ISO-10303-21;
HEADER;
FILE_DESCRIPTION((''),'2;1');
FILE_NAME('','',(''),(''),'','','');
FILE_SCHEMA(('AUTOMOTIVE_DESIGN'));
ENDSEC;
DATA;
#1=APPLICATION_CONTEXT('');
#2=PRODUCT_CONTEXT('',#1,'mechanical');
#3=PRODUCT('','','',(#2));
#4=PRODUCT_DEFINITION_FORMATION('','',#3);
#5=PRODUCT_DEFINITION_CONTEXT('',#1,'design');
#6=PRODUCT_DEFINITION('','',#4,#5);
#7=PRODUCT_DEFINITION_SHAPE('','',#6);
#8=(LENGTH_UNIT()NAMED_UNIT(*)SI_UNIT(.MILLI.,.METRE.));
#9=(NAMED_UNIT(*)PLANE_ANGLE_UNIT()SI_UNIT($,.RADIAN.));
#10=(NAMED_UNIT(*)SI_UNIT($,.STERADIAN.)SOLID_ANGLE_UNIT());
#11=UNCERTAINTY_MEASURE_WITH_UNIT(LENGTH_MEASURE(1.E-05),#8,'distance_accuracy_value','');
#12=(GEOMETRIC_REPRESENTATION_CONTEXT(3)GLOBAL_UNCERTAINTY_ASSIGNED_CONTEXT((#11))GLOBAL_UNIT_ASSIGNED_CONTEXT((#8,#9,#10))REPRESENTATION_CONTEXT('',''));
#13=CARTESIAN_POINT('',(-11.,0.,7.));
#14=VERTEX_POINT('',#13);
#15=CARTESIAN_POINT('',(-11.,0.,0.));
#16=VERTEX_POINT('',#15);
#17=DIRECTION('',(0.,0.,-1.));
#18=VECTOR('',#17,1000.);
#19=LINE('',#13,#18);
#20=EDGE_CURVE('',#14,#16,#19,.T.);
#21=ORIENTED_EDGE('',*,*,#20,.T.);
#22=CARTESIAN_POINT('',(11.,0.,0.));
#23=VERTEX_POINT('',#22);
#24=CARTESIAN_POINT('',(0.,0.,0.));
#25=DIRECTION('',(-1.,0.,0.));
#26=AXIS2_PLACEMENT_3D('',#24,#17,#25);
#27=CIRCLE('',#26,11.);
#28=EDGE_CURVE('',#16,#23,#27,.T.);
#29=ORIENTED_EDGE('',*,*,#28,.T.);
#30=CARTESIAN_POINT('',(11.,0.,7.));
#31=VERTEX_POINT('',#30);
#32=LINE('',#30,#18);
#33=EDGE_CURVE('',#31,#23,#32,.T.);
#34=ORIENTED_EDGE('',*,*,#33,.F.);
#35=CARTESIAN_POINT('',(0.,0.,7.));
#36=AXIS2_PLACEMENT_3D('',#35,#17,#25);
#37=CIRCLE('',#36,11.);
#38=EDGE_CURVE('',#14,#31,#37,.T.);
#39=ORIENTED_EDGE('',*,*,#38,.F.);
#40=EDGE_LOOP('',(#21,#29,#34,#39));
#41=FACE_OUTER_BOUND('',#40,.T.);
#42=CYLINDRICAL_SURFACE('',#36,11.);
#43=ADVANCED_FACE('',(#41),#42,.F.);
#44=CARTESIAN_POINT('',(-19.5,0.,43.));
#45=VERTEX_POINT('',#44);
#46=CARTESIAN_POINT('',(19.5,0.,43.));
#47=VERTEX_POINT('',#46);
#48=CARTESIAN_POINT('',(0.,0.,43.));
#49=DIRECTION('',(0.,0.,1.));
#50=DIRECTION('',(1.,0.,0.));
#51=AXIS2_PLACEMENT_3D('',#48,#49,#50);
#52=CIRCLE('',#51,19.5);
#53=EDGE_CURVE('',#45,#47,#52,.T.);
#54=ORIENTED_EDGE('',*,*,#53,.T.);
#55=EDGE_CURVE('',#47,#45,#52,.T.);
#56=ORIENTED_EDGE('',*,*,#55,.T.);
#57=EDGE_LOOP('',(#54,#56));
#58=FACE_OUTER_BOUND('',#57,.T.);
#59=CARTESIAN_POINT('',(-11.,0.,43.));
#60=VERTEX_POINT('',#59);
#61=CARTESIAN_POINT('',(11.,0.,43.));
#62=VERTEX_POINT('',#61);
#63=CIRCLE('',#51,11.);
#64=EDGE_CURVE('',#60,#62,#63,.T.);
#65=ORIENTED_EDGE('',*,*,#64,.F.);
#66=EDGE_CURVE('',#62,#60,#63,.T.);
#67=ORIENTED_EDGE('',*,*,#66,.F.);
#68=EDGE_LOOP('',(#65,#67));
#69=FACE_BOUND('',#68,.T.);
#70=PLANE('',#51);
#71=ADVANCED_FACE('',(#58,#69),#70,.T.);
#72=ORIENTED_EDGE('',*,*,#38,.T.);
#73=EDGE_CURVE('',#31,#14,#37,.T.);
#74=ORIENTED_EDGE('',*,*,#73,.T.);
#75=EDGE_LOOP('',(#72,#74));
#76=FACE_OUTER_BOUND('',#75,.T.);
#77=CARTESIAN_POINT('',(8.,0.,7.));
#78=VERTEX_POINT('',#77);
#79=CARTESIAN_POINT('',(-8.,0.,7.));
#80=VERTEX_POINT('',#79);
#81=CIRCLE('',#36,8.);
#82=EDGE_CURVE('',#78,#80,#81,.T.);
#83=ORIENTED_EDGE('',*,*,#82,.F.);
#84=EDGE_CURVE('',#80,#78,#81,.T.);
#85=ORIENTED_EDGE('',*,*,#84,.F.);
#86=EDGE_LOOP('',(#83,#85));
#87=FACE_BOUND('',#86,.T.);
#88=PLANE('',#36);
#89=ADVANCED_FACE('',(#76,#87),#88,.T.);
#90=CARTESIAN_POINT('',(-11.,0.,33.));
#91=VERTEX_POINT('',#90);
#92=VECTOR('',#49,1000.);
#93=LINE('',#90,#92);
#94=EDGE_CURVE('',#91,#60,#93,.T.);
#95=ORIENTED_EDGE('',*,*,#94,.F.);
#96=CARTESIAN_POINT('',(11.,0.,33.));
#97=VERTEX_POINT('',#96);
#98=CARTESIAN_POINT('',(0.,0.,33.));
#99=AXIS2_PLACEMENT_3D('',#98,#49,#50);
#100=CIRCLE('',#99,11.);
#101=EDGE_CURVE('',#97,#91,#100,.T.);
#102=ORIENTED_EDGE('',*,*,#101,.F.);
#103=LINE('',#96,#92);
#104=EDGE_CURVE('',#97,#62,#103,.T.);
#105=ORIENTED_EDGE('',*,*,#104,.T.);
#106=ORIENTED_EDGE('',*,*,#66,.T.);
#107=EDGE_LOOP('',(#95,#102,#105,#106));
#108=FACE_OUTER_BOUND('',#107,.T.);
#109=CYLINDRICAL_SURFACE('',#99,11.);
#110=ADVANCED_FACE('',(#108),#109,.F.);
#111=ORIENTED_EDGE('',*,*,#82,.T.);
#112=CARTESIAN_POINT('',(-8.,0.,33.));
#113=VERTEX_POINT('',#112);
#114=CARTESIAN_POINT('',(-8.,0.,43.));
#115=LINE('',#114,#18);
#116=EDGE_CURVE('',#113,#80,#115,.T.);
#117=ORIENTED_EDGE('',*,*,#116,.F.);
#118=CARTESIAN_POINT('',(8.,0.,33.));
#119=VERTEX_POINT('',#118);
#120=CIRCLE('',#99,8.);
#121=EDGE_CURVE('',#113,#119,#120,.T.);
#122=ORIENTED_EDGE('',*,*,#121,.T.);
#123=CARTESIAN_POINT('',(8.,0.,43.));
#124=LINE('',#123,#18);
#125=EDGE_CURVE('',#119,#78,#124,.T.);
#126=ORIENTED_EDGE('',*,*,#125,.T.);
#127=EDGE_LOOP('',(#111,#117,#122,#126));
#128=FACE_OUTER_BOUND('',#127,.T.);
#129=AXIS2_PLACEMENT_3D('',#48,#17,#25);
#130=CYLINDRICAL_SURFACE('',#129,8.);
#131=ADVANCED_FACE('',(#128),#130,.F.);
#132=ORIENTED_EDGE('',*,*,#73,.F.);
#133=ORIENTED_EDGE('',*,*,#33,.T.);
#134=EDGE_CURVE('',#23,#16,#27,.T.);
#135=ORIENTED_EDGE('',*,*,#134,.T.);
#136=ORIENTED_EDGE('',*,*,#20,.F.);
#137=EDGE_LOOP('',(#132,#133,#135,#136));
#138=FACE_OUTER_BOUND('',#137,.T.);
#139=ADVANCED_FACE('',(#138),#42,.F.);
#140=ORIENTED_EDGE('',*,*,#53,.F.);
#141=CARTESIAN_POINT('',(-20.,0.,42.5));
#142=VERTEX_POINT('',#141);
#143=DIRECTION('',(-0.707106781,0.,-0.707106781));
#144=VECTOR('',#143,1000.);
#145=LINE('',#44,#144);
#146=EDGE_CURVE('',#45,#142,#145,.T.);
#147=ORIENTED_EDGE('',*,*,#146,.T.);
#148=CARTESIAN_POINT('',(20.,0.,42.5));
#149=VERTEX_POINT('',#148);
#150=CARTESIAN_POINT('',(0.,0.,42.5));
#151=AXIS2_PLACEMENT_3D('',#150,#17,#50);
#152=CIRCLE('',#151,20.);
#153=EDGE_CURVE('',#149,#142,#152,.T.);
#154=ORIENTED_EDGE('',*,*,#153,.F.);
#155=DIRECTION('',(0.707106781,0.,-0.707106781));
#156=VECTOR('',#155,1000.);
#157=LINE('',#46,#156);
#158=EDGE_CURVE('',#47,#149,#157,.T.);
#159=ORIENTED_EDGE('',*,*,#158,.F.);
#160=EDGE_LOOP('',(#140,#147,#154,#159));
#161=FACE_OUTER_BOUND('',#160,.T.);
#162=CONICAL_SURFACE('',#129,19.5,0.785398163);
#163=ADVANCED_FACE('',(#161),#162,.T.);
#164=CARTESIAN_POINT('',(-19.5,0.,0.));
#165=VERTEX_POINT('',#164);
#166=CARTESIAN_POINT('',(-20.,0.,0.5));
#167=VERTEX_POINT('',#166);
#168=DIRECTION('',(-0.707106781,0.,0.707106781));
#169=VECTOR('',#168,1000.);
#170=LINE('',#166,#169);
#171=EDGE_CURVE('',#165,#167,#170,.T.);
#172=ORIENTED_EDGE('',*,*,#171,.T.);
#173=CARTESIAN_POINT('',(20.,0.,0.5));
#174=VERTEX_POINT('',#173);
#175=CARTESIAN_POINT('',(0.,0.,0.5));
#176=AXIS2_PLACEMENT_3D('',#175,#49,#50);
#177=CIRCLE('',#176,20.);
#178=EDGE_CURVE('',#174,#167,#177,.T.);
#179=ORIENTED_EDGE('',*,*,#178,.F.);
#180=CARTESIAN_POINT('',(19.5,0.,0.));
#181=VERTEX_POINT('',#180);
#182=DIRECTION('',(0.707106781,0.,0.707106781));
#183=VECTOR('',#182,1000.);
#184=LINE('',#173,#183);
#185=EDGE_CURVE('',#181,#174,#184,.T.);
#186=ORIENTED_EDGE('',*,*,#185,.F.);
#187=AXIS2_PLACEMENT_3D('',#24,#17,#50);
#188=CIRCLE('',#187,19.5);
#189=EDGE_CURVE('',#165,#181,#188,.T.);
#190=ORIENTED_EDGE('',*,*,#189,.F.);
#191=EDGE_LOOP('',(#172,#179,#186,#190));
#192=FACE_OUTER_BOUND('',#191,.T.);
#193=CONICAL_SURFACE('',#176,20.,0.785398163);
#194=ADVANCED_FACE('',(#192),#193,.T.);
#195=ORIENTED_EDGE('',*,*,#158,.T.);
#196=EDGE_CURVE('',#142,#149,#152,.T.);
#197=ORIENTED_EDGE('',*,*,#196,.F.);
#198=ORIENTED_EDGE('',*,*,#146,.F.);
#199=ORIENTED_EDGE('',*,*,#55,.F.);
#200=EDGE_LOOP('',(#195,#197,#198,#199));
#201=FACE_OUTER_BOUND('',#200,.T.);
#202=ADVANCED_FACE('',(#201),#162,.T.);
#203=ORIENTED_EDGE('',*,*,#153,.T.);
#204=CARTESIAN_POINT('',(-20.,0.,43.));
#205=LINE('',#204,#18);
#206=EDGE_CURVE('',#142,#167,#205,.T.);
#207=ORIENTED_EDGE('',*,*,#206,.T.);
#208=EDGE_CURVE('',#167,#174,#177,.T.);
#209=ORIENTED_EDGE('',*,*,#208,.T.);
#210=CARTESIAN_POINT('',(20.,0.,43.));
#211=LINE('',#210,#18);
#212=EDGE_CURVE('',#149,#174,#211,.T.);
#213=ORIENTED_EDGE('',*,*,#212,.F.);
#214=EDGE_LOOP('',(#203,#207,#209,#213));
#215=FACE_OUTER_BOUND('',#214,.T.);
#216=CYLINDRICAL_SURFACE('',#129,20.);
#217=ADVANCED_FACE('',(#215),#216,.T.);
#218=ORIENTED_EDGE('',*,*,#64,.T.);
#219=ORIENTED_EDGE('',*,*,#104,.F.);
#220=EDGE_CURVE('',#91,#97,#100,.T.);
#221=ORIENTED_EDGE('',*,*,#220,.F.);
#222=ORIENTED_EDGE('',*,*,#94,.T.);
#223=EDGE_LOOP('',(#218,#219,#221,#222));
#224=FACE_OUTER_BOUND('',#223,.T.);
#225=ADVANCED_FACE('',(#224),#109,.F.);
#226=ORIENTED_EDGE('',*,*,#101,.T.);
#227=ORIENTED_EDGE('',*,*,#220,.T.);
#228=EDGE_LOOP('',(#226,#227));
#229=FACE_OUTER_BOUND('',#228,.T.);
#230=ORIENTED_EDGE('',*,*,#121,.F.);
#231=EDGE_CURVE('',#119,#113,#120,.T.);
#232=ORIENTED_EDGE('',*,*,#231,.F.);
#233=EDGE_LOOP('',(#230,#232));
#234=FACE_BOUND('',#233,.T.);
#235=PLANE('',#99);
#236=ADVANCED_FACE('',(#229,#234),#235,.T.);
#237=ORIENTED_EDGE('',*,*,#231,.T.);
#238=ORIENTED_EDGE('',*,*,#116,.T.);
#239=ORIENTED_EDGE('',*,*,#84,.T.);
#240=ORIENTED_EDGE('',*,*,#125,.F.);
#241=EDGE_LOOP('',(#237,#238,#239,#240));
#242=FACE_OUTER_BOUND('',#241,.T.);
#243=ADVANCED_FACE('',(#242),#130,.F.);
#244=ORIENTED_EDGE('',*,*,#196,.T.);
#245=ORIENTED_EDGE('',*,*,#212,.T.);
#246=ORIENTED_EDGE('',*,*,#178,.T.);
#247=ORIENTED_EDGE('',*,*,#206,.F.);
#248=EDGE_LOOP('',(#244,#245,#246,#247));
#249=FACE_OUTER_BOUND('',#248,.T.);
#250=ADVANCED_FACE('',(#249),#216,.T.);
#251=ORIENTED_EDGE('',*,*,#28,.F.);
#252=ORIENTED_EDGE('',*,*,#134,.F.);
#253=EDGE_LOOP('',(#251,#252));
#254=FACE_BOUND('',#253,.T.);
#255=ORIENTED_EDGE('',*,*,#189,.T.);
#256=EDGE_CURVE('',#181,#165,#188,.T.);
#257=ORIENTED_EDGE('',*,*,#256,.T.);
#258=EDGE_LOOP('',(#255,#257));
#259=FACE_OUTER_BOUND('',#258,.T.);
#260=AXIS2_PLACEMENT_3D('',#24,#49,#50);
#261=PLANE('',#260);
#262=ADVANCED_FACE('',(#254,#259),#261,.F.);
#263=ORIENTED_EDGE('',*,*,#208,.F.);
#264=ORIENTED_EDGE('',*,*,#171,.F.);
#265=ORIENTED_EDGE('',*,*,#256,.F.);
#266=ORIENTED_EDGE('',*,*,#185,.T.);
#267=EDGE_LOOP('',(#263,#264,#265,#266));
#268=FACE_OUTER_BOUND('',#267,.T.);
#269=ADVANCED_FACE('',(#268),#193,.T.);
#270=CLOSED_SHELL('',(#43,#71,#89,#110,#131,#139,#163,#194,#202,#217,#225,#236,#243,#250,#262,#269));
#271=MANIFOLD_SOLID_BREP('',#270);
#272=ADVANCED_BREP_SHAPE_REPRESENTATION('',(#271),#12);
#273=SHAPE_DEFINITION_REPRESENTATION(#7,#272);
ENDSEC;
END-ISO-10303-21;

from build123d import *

# Parameters (mm, degrees)
SKETCH_1_R          = 20
EXTRUDE_1_DEPTH     = 43
SKETCH_2_R          = 11
CUT_EXTRUDE_1_DEPTH = 10
CUT_EXTRUDE_START   = -7
SKETCH_3_R          = 11
CUT_EXTRUDE_2_DEPTH = 7
SKETCH_4_R          = 8
CUT_EXTRUDE_3_DEPTH = 46.782092569
CHAMFER_1_SIZE      = 0.5


with BuildPart() as part:
    # 草图1 → 凸台-拉伸1 (new body)
    with BuildSketch(Plane.XY):
        Circle(SKETCH_1_R)
    extrude(amount=EXTRUDE_1_DEPTH)

    # 草图2 → 切除-拉伸1 (cut)
    with BuildSketch(Plane.XY.offset(43)):
        Circle(SKETCH_2_R)
    extrude(amount=-CUT_EXTRUDE_1_DEPTH, mode=Mode.SUBTRACT)

    # 草图3 → 切除-拉伸2 (cut)
    with BuildSketch(Plane(origin=(0, 0, 0), x_dir=(-1, 0, 0), z_dir=(0, 0, -1)).offset(CUT_EXTRUDE_START)):
        with Locations(Location((0, 0, 0), (0, 0, 180))):
            Circle(SKETCH_3_R)
    extrude(amount=CUT_EXTRUDE_2_DEPTH, mode=Mode.SUBTRACT)

    # 草图4 → 切除-拉伸3 (cut, through all)
    with BuildSketch(Plane(origin=(0, 0, 7), x_dir=(-1, 0, 0), z_dir=(0, 0, -1))):
        Circle(SKETCH_4_R)
    extrude(amount=-CUT_EXTRUDE_3_DEPTH, mode=Mode.SUBTRACT)

    # 倒角1
    chamfer_1_edges = [part.edges().sort_by_distance(p)[0] for p in [
        (-20, 0, 0),
        (-20, 0, 43),
    ]]
    chamfer(chamfer_1_edges, length=CHAMFER_1_SIZE)


solid = part.part
